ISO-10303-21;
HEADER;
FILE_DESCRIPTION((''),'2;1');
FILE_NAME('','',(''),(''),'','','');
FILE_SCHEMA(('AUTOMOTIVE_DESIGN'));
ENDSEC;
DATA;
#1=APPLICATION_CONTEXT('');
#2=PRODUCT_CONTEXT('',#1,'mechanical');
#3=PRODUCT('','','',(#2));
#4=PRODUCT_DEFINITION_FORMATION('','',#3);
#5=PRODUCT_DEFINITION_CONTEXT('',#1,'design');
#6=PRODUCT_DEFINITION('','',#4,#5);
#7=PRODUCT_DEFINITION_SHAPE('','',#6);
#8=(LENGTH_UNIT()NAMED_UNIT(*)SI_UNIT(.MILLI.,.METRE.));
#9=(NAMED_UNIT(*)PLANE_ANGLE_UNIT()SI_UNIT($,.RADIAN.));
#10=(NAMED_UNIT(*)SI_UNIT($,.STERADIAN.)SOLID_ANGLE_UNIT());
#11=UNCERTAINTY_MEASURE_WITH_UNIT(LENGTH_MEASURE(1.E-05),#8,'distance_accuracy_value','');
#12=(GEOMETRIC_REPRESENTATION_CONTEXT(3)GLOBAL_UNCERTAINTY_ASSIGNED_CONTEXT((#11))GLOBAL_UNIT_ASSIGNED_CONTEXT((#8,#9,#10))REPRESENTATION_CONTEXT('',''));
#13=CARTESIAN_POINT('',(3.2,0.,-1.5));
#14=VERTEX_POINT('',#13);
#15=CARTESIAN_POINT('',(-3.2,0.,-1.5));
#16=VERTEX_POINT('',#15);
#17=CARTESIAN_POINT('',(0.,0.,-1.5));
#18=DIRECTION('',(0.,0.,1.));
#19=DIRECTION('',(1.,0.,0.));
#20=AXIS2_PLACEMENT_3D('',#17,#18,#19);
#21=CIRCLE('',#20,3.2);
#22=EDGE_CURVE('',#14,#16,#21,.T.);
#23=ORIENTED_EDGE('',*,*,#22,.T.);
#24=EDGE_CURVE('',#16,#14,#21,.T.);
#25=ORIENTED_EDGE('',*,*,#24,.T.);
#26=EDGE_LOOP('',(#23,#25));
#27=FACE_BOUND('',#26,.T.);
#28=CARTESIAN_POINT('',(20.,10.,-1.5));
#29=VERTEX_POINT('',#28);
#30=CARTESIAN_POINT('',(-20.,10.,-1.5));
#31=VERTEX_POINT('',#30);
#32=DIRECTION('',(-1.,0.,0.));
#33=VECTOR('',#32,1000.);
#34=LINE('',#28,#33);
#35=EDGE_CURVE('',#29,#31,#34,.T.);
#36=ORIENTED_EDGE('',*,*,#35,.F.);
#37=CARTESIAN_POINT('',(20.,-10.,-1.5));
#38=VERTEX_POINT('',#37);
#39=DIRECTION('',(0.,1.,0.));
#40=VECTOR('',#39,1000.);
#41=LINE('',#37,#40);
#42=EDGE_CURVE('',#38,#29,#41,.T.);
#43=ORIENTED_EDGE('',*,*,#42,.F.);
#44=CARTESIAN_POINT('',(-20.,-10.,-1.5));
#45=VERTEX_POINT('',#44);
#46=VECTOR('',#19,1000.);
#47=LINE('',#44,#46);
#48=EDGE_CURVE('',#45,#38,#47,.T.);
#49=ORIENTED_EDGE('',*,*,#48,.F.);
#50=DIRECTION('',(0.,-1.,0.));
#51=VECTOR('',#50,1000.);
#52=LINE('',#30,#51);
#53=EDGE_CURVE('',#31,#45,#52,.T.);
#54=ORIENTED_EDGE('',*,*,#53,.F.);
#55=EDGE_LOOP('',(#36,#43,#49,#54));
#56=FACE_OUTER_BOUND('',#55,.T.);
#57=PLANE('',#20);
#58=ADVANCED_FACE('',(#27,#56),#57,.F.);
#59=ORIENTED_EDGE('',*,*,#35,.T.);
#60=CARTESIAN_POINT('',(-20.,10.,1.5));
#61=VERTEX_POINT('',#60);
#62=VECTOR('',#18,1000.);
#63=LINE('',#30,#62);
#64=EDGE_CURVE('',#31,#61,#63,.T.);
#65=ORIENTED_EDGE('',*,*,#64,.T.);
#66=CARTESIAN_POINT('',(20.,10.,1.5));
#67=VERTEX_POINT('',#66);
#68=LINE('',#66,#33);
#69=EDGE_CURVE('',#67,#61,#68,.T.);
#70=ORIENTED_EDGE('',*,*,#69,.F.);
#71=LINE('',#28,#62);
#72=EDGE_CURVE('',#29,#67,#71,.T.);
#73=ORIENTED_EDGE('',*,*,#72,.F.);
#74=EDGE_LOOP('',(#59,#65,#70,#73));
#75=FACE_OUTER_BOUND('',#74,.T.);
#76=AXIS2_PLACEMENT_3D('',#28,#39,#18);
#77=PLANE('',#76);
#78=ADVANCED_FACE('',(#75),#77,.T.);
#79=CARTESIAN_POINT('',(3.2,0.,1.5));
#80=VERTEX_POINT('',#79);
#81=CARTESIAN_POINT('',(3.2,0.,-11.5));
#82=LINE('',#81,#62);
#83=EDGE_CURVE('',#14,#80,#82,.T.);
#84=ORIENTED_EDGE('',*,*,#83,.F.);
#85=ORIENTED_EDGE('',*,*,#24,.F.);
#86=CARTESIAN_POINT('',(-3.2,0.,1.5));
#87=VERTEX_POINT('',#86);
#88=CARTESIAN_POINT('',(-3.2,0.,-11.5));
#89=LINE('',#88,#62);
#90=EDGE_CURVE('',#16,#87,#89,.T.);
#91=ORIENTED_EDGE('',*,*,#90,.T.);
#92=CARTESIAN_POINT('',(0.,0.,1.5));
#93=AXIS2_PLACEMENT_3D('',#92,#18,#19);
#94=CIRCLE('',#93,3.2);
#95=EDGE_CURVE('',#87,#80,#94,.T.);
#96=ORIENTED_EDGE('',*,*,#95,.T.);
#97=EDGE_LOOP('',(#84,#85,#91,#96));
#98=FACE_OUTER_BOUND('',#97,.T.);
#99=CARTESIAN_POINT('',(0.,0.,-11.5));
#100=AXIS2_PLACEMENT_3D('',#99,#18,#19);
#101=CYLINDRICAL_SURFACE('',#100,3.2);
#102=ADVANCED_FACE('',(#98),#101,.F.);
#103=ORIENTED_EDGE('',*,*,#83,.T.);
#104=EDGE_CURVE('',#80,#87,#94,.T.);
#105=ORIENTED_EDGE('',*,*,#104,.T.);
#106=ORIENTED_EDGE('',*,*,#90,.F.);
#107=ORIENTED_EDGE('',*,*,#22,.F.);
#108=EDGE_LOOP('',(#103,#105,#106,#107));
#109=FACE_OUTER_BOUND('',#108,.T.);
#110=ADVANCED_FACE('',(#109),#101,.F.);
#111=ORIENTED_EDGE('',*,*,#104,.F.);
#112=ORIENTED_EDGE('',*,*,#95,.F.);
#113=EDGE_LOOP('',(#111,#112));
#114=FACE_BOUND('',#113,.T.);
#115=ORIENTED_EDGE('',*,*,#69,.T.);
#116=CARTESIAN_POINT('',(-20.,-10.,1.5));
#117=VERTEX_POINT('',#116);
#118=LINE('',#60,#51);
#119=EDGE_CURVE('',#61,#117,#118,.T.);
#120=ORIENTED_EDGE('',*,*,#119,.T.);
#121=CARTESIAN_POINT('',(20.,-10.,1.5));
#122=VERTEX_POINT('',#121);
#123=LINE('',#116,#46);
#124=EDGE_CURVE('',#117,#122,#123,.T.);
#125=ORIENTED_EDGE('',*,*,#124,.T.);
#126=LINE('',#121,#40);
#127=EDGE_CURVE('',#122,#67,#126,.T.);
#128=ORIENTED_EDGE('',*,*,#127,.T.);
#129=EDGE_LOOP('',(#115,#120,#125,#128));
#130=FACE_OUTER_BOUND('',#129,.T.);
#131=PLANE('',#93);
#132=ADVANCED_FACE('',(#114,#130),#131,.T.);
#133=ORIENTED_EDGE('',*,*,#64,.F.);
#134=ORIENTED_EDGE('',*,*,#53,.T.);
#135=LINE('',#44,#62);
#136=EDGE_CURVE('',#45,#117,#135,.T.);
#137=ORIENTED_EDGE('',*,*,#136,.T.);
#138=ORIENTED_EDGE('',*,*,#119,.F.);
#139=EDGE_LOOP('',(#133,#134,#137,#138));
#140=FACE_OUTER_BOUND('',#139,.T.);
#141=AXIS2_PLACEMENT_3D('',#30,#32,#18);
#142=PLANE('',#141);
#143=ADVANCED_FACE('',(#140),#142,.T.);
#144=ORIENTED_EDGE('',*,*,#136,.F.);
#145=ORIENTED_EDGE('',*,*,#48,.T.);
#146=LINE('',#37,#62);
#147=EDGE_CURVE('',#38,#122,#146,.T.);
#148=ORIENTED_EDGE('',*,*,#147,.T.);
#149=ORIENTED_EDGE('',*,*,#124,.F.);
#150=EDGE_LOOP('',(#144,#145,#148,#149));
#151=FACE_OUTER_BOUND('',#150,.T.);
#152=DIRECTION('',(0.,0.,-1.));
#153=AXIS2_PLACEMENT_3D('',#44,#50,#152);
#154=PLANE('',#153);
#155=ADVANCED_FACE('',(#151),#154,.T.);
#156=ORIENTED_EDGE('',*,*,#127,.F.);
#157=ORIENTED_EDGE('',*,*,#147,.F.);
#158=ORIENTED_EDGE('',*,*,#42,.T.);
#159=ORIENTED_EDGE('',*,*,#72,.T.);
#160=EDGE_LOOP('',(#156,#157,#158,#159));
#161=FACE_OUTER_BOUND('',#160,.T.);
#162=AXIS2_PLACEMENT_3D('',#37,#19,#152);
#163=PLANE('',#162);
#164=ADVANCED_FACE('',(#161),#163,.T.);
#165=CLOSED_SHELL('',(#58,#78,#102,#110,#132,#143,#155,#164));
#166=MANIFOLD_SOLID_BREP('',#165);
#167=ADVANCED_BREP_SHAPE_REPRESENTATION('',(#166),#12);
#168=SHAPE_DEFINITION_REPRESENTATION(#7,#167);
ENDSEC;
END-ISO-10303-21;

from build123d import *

# Parameters (mm, degrees)
SKETCH_1_W          = 40
SKETCH_1_H          = 20
EXTRUDE_1_DEPTH     = 1.5
SKETCH_2_R          = 3.2
CUT_EXTRUDE_1_DEPTH = 11.5


with BuildPart() as part:
    # 草图1 → 凸台-拉伸1 (new, symmetric)
    with BuildSketch(Plane.XY):
        Rectangle(SKETCH_1_W, SKETCH_1_H)
    extrude(amount=EXTRUDE_1_DEPTH, both=True)

    # 草图2 → 切除-拉伸1 (cut, symmetric)
    with BuildSketch(Plane.XY):
        Circle(SKETCH_2_R)
    extrude(amount=CUT_EXTRUDE_1_DEPTH, both=True, mode=Mode.SUBTRACT)


solid = part.part
